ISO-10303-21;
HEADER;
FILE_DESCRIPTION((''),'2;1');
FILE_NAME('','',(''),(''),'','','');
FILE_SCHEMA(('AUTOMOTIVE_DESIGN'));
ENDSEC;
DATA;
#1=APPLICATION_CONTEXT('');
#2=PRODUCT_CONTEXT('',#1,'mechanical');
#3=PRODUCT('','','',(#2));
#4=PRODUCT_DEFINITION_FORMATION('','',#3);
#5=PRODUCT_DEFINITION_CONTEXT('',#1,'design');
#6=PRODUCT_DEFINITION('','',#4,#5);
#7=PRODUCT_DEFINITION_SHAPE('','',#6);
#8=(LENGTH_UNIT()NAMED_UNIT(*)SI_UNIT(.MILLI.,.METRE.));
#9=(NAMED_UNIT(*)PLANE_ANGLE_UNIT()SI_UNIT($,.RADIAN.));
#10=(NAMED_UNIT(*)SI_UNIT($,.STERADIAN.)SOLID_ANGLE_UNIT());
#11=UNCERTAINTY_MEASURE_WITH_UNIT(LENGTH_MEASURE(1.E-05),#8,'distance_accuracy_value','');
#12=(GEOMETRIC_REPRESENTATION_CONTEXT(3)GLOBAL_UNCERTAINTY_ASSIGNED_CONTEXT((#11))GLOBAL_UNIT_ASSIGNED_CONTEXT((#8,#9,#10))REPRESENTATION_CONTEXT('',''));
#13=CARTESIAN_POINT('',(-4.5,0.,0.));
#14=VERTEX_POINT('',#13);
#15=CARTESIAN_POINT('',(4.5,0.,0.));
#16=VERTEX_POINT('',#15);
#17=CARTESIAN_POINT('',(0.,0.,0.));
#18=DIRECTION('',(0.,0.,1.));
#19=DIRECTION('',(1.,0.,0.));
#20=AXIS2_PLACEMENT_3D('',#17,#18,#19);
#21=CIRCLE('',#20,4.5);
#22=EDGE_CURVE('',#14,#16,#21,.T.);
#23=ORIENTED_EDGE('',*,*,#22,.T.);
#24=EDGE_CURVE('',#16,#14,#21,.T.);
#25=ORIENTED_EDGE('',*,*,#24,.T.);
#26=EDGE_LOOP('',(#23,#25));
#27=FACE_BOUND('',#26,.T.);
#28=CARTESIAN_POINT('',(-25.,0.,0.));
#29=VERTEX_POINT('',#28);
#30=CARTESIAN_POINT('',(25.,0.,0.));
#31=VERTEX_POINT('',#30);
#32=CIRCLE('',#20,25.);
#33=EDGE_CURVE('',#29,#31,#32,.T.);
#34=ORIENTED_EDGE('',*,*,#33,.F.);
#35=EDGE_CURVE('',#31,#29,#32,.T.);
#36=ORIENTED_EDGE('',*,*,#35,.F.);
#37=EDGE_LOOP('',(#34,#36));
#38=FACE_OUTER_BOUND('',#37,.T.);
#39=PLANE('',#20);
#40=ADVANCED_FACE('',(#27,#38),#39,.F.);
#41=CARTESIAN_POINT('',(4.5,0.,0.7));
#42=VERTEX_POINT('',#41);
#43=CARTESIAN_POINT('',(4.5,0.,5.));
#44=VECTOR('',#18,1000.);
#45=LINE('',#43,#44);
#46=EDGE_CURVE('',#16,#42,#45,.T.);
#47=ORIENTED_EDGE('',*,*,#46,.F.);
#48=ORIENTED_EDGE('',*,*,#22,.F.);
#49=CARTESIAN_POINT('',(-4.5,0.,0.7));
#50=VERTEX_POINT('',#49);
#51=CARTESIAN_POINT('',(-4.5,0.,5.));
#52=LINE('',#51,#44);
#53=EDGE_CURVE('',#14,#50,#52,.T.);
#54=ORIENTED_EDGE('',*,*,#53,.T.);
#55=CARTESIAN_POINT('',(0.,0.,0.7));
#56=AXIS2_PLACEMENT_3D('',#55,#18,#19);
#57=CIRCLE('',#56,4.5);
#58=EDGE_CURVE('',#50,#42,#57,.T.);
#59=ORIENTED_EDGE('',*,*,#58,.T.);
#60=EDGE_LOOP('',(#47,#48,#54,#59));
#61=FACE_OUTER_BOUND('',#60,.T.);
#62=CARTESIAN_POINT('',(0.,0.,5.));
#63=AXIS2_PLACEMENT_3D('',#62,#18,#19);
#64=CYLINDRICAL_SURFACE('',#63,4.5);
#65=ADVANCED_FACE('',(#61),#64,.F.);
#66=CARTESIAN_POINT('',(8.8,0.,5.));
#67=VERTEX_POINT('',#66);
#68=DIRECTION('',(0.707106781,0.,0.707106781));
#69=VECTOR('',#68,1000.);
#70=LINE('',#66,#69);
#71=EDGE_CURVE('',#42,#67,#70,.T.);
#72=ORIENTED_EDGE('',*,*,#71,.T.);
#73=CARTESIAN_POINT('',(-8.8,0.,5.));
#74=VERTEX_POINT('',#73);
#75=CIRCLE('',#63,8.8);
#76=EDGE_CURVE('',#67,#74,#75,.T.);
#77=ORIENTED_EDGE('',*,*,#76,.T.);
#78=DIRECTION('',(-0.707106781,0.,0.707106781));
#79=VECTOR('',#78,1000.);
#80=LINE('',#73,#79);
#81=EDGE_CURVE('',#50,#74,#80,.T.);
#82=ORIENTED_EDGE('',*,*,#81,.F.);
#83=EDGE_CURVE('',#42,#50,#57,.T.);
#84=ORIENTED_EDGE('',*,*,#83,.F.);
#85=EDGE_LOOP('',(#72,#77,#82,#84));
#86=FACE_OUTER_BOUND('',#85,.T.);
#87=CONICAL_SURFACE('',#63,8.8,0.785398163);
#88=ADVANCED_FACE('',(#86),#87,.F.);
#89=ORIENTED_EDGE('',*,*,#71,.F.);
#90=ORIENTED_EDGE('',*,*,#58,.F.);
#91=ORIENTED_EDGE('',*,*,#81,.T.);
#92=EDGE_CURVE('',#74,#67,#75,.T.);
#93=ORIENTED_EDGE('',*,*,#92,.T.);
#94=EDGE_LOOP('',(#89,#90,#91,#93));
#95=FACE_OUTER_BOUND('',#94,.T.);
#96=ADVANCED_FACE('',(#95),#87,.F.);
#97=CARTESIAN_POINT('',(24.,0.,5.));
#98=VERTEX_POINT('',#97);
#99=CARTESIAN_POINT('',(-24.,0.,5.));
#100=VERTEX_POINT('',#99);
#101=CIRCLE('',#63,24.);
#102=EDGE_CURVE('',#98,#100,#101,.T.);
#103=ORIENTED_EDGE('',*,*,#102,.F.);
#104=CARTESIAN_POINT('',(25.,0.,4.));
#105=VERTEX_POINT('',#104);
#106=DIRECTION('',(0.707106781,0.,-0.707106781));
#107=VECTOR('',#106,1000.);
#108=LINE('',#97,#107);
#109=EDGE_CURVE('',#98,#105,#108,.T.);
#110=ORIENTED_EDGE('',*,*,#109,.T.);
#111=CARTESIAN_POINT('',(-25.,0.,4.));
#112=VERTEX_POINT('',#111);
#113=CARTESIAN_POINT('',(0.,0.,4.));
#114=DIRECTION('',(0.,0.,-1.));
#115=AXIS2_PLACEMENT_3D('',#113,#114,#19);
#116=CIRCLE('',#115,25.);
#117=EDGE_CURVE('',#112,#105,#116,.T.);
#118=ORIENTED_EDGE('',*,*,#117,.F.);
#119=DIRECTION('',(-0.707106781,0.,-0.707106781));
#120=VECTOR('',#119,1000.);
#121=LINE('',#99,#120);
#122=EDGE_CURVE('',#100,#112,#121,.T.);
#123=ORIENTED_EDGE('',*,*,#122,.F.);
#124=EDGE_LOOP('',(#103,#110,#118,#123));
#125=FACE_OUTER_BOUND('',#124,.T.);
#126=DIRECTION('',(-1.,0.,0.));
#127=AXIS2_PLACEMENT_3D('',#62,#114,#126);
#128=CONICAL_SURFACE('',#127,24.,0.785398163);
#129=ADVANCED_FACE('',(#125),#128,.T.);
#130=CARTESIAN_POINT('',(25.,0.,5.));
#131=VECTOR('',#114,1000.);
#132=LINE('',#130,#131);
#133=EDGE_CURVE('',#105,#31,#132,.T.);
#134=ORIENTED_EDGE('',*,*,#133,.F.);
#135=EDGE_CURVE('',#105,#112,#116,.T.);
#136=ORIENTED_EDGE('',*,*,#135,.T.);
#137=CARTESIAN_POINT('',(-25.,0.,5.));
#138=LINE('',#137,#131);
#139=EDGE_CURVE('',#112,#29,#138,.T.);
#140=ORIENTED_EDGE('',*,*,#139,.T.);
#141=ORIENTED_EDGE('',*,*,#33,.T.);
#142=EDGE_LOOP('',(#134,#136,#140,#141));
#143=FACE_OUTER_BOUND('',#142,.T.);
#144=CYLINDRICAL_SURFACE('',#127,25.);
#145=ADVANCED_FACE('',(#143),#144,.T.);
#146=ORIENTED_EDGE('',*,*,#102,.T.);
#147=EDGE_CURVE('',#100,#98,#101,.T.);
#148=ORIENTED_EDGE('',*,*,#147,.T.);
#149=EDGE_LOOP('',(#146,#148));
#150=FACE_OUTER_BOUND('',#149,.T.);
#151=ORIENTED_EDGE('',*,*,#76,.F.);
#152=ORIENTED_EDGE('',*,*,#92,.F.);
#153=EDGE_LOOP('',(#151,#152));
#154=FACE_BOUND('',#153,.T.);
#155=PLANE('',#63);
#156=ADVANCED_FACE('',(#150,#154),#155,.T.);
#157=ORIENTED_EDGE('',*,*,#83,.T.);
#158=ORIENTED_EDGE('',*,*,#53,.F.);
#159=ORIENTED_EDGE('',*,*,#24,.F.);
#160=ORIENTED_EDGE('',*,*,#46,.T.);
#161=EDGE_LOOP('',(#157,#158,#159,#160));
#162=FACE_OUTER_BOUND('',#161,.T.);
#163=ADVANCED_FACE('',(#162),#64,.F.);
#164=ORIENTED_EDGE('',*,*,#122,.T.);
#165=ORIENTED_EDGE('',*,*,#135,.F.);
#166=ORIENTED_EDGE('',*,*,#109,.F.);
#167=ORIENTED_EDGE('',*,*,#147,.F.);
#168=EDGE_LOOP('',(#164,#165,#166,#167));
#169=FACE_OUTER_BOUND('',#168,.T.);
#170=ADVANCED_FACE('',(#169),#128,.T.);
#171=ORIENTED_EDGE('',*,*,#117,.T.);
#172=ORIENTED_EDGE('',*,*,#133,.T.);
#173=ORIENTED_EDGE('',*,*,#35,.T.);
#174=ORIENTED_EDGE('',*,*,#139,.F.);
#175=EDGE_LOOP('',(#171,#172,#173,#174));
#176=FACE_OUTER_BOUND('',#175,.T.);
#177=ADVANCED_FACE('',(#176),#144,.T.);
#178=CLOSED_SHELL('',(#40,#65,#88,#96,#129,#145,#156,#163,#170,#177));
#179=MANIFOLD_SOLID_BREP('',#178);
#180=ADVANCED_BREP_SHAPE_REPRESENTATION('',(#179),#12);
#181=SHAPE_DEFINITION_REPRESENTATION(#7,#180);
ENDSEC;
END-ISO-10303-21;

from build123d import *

# Parameters (mm, degrees)
SKETCH_1_R      = 25
EXTRUDE_1_DEPTH = 5
CHAMFER_1_SIZE  = 1


with BuildPart() as part:
    # 草图1 → 凸台-拉伸1 (new body)
    with BuildSketch(Plane.XY):
        Circle(SKETCH_1_R)
    extrude(amount=EXTRUDE_1_DEPTH)

    # 草图3 → 打孔尺寸(%根据)内六角花形半沉头螺钉的类型1 (revolve, cut)
    with BuildSketch(Plane(origin=(0, 0, 5), x_dir=(0, -1, 0), z_dir=(1, 0, 0))):
        Polygon((0, 0), (0, 5), (4.5, 5), (4.5, 4.3), (8.8, 0), align=None)
    revolve(axis=Axis((0, 0, 11.35), (0, 0, -1)), mode=Mode.SUBTRACT)

    # 倒角1
    chamfer_1_edges = [part.edges().sort_by_distance(p)[0] for p in [
        (-25, 0, 5),
    ]]
    chamfer(chamfer_1_edges, length=CHAMFER_1_SIZE)


solid = part.part
